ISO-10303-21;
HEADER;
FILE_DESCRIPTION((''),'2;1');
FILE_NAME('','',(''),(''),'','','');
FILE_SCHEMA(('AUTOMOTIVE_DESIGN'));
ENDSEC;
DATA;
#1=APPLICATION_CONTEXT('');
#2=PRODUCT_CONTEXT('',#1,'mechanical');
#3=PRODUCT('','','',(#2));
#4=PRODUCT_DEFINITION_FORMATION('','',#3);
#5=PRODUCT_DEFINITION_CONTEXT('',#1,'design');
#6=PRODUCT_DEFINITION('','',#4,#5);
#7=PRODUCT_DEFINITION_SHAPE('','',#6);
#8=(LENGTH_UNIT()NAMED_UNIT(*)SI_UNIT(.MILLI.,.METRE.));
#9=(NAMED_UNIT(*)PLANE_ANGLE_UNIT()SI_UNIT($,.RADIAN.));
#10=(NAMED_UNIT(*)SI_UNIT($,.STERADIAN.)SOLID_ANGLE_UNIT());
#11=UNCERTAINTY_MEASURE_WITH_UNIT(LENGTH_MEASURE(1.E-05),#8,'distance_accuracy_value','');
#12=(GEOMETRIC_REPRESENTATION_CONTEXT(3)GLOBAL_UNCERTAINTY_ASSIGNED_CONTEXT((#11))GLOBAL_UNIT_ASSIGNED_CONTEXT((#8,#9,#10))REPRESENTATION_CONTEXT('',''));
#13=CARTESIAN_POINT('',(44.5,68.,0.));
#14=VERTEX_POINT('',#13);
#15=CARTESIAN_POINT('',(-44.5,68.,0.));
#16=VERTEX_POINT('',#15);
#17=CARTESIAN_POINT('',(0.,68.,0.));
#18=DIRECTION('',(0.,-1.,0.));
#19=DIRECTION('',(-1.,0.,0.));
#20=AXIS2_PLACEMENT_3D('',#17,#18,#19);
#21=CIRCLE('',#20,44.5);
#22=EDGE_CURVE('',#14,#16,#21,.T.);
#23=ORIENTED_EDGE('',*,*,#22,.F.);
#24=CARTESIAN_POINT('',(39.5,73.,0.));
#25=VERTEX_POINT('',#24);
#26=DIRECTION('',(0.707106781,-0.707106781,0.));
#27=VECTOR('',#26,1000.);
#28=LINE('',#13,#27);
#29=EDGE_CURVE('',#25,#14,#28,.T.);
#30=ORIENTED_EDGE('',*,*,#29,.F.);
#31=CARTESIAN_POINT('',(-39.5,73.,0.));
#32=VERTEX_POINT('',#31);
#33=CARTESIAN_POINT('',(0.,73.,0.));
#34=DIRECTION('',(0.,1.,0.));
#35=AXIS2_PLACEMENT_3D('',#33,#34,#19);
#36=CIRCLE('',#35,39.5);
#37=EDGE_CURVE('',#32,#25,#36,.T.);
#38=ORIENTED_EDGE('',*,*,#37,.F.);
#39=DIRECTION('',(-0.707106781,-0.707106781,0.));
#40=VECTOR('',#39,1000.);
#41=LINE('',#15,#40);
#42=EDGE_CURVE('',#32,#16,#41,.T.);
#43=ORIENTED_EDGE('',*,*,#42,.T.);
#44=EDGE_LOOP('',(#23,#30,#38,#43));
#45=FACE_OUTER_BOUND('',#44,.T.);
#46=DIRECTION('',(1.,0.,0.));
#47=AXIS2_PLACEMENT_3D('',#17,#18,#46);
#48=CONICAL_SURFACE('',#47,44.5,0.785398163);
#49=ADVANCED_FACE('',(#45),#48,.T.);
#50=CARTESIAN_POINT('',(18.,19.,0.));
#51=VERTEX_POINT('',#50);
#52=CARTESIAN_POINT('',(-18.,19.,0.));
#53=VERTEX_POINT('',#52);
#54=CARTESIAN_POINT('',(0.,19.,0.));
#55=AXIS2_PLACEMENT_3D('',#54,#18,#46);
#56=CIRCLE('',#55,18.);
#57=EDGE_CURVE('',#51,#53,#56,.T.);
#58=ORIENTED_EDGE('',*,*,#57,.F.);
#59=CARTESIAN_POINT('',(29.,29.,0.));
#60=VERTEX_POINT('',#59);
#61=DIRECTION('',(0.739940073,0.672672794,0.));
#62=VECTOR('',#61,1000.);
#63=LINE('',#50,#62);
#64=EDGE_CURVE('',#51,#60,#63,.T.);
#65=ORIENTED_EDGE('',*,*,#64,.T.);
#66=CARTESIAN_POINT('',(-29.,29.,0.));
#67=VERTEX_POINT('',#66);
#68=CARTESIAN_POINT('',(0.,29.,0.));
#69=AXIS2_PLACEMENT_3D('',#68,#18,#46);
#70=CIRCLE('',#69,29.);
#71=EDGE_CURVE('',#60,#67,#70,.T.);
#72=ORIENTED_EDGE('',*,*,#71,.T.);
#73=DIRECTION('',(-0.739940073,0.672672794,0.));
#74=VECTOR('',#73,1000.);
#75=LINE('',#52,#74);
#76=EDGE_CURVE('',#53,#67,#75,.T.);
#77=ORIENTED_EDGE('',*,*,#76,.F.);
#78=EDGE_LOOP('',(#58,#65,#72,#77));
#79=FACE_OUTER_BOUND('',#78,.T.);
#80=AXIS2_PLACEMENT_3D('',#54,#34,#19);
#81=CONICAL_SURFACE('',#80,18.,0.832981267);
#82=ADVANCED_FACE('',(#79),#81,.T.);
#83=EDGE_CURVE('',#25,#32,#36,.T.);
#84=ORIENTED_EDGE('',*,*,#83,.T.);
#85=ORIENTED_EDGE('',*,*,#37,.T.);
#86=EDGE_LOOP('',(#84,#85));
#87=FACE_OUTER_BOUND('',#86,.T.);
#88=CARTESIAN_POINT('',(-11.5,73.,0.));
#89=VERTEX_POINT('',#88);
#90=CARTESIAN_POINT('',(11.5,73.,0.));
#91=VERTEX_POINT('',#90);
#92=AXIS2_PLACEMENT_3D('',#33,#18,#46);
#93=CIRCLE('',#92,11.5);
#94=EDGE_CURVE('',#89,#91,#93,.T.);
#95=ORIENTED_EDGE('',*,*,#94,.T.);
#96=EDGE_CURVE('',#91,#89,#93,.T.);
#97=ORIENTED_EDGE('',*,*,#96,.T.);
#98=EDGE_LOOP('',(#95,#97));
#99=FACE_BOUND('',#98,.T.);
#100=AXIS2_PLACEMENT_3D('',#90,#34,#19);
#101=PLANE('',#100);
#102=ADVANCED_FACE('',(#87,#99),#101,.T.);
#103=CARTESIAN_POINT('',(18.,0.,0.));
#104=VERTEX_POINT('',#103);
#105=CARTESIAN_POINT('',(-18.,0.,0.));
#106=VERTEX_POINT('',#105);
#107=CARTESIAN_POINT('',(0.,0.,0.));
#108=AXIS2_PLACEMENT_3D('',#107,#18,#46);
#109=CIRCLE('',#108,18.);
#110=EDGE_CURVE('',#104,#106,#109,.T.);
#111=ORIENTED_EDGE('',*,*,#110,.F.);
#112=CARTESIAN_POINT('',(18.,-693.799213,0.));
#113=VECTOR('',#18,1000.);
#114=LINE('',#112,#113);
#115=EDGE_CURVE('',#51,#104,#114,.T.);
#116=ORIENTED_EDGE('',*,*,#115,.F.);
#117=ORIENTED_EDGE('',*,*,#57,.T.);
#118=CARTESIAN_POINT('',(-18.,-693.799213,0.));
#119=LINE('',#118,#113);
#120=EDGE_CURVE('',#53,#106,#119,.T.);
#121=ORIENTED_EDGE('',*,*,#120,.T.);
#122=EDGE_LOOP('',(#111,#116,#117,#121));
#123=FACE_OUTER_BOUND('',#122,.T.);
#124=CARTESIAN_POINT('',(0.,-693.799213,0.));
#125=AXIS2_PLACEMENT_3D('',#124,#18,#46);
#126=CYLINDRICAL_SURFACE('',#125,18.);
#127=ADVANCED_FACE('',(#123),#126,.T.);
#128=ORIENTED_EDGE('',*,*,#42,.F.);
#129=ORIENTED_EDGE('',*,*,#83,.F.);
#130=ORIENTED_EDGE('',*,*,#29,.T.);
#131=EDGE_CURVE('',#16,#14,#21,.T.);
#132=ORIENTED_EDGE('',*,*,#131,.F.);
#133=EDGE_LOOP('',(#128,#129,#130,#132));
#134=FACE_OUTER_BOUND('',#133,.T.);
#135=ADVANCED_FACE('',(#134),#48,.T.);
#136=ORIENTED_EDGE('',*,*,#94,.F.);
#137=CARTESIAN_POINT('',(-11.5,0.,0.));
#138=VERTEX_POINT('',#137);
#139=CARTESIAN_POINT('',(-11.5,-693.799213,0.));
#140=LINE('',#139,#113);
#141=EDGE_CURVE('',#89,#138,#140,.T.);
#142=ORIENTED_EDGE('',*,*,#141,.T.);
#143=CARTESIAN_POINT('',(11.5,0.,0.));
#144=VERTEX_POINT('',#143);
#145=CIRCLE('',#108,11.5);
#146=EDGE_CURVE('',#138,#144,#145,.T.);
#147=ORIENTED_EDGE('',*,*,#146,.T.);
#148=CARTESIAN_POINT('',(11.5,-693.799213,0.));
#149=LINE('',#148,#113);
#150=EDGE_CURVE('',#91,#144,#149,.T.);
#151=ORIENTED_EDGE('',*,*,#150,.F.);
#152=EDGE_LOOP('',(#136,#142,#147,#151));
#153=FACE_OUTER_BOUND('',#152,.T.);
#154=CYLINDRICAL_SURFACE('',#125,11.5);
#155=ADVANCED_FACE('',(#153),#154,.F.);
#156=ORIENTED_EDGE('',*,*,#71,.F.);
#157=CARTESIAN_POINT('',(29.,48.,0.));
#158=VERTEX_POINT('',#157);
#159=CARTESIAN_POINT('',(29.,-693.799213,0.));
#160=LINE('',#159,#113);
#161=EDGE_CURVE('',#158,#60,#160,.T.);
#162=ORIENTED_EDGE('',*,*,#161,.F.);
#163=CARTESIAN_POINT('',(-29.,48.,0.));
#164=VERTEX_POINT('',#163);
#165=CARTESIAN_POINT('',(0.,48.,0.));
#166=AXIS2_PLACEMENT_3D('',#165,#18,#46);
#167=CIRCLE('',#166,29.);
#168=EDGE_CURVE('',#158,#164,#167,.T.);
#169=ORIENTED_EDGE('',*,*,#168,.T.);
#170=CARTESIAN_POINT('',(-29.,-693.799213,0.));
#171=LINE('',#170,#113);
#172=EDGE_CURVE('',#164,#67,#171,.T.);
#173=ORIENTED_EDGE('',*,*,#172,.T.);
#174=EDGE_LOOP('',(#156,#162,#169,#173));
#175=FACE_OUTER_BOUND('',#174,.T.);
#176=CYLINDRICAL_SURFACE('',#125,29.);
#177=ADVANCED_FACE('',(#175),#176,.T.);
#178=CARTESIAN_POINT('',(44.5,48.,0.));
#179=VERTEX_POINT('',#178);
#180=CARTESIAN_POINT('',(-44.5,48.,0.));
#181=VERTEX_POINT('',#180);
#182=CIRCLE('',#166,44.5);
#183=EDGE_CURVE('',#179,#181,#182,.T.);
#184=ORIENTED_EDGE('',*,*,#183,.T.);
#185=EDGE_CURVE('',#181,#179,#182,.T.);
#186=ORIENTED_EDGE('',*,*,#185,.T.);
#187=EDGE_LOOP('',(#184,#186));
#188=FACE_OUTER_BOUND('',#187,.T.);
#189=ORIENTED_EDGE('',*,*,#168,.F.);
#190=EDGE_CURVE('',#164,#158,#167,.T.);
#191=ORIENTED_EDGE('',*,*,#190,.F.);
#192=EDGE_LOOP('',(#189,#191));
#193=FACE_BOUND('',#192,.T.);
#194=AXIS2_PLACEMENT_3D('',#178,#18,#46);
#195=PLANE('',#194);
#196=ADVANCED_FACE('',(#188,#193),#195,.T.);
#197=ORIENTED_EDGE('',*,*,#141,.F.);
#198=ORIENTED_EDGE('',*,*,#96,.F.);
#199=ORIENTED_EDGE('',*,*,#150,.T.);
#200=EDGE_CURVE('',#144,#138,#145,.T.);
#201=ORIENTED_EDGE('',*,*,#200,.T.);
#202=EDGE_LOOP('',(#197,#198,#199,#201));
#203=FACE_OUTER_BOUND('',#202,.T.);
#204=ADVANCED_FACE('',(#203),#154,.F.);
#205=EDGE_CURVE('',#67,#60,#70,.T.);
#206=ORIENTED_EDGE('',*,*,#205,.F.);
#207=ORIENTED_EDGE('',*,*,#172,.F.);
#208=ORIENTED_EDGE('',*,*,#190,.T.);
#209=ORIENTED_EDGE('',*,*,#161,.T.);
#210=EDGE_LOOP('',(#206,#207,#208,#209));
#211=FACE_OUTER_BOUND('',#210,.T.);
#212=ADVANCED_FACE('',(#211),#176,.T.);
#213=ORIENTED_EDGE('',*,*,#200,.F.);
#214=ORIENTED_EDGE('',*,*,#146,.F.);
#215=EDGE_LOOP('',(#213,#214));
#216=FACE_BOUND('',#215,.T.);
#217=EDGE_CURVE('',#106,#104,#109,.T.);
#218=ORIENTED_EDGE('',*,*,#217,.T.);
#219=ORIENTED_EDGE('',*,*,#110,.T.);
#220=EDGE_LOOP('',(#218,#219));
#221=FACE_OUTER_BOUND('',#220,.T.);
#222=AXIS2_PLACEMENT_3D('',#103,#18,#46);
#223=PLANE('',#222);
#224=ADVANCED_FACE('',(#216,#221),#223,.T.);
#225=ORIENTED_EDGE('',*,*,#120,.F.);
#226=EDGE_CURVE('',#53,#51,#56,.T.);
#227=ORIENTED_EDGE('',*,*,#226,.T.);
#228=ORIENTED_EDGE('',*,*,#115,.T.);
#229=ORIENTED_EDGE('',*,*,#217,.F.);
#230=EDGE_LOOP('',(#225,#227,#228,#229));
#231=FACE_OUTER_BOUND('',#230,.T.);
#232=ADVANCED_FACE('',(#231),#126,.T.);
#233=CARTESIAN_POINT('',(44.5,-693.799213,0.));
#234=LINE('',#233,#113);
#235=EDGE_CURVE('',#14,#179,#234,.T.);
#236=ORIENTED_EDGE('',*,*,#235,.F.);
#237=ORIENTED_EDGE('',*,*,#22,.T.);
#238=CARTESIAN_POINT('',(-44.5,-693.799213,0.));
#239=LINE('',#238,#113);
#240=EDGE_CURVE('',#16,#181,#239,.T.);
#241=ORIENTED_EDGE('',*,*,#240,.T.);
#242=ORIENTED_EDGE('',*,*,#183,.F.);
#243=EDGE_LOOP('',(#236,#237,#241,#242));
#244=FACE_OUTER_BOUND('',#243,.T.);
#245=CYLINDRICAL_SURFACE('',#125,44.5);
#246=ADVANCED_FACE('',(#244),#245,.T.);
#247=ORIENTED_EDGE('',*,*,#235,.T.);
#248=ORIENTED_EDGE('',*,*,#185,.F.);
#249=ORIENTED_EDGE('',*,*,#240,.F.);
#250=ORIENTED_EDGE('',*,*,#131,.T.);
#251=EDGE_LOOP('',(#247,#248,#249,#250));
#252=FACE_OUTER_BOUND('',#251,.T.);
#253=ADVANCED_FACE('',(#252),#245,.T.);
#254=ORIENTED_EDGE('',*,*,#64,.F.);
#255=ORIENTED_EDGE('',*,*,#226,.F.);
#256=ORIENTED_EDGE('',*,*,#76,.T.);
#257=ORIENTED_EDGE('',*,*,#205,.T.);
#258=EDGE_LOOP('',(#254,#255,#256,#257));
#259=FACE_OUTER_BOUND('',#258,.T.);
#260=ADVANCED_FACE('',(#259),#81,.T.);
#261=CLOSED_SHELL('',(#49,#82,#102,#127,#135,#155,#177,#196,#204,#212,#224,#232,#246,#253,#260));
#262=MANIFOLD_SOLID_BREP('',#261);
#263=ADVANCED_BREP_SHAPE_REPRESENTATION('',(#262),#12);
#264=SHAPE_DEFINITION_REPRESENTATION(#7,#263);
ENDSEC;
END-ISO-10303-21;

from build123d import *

# Parameters (mm, degrees)
CHAMFER1_SIZE = 5


with BuildPart() as part:
    # Sketch1 → Revolve1 (revolve)
    with BuildSketch(Plane.XY):
        Polygon((11.5, 0), (11.5, 73), (44.5, 73), (44.5, 48), (29, 48), (29, 29), (18, 19), (18, 0), align=None)
    revolve(axis=Axis((0, -693.799212598, 0), (0, 1, 0)))

    # Chamfer1
    chamfer1_edges = [part.edges().sort_by_distance(p)[0] for p in [
        (-44.5, 73, 0),
    ]]
    chamfer(chamfer1_edges, length=CHAMFER1_SIZE)


solid = part.part
